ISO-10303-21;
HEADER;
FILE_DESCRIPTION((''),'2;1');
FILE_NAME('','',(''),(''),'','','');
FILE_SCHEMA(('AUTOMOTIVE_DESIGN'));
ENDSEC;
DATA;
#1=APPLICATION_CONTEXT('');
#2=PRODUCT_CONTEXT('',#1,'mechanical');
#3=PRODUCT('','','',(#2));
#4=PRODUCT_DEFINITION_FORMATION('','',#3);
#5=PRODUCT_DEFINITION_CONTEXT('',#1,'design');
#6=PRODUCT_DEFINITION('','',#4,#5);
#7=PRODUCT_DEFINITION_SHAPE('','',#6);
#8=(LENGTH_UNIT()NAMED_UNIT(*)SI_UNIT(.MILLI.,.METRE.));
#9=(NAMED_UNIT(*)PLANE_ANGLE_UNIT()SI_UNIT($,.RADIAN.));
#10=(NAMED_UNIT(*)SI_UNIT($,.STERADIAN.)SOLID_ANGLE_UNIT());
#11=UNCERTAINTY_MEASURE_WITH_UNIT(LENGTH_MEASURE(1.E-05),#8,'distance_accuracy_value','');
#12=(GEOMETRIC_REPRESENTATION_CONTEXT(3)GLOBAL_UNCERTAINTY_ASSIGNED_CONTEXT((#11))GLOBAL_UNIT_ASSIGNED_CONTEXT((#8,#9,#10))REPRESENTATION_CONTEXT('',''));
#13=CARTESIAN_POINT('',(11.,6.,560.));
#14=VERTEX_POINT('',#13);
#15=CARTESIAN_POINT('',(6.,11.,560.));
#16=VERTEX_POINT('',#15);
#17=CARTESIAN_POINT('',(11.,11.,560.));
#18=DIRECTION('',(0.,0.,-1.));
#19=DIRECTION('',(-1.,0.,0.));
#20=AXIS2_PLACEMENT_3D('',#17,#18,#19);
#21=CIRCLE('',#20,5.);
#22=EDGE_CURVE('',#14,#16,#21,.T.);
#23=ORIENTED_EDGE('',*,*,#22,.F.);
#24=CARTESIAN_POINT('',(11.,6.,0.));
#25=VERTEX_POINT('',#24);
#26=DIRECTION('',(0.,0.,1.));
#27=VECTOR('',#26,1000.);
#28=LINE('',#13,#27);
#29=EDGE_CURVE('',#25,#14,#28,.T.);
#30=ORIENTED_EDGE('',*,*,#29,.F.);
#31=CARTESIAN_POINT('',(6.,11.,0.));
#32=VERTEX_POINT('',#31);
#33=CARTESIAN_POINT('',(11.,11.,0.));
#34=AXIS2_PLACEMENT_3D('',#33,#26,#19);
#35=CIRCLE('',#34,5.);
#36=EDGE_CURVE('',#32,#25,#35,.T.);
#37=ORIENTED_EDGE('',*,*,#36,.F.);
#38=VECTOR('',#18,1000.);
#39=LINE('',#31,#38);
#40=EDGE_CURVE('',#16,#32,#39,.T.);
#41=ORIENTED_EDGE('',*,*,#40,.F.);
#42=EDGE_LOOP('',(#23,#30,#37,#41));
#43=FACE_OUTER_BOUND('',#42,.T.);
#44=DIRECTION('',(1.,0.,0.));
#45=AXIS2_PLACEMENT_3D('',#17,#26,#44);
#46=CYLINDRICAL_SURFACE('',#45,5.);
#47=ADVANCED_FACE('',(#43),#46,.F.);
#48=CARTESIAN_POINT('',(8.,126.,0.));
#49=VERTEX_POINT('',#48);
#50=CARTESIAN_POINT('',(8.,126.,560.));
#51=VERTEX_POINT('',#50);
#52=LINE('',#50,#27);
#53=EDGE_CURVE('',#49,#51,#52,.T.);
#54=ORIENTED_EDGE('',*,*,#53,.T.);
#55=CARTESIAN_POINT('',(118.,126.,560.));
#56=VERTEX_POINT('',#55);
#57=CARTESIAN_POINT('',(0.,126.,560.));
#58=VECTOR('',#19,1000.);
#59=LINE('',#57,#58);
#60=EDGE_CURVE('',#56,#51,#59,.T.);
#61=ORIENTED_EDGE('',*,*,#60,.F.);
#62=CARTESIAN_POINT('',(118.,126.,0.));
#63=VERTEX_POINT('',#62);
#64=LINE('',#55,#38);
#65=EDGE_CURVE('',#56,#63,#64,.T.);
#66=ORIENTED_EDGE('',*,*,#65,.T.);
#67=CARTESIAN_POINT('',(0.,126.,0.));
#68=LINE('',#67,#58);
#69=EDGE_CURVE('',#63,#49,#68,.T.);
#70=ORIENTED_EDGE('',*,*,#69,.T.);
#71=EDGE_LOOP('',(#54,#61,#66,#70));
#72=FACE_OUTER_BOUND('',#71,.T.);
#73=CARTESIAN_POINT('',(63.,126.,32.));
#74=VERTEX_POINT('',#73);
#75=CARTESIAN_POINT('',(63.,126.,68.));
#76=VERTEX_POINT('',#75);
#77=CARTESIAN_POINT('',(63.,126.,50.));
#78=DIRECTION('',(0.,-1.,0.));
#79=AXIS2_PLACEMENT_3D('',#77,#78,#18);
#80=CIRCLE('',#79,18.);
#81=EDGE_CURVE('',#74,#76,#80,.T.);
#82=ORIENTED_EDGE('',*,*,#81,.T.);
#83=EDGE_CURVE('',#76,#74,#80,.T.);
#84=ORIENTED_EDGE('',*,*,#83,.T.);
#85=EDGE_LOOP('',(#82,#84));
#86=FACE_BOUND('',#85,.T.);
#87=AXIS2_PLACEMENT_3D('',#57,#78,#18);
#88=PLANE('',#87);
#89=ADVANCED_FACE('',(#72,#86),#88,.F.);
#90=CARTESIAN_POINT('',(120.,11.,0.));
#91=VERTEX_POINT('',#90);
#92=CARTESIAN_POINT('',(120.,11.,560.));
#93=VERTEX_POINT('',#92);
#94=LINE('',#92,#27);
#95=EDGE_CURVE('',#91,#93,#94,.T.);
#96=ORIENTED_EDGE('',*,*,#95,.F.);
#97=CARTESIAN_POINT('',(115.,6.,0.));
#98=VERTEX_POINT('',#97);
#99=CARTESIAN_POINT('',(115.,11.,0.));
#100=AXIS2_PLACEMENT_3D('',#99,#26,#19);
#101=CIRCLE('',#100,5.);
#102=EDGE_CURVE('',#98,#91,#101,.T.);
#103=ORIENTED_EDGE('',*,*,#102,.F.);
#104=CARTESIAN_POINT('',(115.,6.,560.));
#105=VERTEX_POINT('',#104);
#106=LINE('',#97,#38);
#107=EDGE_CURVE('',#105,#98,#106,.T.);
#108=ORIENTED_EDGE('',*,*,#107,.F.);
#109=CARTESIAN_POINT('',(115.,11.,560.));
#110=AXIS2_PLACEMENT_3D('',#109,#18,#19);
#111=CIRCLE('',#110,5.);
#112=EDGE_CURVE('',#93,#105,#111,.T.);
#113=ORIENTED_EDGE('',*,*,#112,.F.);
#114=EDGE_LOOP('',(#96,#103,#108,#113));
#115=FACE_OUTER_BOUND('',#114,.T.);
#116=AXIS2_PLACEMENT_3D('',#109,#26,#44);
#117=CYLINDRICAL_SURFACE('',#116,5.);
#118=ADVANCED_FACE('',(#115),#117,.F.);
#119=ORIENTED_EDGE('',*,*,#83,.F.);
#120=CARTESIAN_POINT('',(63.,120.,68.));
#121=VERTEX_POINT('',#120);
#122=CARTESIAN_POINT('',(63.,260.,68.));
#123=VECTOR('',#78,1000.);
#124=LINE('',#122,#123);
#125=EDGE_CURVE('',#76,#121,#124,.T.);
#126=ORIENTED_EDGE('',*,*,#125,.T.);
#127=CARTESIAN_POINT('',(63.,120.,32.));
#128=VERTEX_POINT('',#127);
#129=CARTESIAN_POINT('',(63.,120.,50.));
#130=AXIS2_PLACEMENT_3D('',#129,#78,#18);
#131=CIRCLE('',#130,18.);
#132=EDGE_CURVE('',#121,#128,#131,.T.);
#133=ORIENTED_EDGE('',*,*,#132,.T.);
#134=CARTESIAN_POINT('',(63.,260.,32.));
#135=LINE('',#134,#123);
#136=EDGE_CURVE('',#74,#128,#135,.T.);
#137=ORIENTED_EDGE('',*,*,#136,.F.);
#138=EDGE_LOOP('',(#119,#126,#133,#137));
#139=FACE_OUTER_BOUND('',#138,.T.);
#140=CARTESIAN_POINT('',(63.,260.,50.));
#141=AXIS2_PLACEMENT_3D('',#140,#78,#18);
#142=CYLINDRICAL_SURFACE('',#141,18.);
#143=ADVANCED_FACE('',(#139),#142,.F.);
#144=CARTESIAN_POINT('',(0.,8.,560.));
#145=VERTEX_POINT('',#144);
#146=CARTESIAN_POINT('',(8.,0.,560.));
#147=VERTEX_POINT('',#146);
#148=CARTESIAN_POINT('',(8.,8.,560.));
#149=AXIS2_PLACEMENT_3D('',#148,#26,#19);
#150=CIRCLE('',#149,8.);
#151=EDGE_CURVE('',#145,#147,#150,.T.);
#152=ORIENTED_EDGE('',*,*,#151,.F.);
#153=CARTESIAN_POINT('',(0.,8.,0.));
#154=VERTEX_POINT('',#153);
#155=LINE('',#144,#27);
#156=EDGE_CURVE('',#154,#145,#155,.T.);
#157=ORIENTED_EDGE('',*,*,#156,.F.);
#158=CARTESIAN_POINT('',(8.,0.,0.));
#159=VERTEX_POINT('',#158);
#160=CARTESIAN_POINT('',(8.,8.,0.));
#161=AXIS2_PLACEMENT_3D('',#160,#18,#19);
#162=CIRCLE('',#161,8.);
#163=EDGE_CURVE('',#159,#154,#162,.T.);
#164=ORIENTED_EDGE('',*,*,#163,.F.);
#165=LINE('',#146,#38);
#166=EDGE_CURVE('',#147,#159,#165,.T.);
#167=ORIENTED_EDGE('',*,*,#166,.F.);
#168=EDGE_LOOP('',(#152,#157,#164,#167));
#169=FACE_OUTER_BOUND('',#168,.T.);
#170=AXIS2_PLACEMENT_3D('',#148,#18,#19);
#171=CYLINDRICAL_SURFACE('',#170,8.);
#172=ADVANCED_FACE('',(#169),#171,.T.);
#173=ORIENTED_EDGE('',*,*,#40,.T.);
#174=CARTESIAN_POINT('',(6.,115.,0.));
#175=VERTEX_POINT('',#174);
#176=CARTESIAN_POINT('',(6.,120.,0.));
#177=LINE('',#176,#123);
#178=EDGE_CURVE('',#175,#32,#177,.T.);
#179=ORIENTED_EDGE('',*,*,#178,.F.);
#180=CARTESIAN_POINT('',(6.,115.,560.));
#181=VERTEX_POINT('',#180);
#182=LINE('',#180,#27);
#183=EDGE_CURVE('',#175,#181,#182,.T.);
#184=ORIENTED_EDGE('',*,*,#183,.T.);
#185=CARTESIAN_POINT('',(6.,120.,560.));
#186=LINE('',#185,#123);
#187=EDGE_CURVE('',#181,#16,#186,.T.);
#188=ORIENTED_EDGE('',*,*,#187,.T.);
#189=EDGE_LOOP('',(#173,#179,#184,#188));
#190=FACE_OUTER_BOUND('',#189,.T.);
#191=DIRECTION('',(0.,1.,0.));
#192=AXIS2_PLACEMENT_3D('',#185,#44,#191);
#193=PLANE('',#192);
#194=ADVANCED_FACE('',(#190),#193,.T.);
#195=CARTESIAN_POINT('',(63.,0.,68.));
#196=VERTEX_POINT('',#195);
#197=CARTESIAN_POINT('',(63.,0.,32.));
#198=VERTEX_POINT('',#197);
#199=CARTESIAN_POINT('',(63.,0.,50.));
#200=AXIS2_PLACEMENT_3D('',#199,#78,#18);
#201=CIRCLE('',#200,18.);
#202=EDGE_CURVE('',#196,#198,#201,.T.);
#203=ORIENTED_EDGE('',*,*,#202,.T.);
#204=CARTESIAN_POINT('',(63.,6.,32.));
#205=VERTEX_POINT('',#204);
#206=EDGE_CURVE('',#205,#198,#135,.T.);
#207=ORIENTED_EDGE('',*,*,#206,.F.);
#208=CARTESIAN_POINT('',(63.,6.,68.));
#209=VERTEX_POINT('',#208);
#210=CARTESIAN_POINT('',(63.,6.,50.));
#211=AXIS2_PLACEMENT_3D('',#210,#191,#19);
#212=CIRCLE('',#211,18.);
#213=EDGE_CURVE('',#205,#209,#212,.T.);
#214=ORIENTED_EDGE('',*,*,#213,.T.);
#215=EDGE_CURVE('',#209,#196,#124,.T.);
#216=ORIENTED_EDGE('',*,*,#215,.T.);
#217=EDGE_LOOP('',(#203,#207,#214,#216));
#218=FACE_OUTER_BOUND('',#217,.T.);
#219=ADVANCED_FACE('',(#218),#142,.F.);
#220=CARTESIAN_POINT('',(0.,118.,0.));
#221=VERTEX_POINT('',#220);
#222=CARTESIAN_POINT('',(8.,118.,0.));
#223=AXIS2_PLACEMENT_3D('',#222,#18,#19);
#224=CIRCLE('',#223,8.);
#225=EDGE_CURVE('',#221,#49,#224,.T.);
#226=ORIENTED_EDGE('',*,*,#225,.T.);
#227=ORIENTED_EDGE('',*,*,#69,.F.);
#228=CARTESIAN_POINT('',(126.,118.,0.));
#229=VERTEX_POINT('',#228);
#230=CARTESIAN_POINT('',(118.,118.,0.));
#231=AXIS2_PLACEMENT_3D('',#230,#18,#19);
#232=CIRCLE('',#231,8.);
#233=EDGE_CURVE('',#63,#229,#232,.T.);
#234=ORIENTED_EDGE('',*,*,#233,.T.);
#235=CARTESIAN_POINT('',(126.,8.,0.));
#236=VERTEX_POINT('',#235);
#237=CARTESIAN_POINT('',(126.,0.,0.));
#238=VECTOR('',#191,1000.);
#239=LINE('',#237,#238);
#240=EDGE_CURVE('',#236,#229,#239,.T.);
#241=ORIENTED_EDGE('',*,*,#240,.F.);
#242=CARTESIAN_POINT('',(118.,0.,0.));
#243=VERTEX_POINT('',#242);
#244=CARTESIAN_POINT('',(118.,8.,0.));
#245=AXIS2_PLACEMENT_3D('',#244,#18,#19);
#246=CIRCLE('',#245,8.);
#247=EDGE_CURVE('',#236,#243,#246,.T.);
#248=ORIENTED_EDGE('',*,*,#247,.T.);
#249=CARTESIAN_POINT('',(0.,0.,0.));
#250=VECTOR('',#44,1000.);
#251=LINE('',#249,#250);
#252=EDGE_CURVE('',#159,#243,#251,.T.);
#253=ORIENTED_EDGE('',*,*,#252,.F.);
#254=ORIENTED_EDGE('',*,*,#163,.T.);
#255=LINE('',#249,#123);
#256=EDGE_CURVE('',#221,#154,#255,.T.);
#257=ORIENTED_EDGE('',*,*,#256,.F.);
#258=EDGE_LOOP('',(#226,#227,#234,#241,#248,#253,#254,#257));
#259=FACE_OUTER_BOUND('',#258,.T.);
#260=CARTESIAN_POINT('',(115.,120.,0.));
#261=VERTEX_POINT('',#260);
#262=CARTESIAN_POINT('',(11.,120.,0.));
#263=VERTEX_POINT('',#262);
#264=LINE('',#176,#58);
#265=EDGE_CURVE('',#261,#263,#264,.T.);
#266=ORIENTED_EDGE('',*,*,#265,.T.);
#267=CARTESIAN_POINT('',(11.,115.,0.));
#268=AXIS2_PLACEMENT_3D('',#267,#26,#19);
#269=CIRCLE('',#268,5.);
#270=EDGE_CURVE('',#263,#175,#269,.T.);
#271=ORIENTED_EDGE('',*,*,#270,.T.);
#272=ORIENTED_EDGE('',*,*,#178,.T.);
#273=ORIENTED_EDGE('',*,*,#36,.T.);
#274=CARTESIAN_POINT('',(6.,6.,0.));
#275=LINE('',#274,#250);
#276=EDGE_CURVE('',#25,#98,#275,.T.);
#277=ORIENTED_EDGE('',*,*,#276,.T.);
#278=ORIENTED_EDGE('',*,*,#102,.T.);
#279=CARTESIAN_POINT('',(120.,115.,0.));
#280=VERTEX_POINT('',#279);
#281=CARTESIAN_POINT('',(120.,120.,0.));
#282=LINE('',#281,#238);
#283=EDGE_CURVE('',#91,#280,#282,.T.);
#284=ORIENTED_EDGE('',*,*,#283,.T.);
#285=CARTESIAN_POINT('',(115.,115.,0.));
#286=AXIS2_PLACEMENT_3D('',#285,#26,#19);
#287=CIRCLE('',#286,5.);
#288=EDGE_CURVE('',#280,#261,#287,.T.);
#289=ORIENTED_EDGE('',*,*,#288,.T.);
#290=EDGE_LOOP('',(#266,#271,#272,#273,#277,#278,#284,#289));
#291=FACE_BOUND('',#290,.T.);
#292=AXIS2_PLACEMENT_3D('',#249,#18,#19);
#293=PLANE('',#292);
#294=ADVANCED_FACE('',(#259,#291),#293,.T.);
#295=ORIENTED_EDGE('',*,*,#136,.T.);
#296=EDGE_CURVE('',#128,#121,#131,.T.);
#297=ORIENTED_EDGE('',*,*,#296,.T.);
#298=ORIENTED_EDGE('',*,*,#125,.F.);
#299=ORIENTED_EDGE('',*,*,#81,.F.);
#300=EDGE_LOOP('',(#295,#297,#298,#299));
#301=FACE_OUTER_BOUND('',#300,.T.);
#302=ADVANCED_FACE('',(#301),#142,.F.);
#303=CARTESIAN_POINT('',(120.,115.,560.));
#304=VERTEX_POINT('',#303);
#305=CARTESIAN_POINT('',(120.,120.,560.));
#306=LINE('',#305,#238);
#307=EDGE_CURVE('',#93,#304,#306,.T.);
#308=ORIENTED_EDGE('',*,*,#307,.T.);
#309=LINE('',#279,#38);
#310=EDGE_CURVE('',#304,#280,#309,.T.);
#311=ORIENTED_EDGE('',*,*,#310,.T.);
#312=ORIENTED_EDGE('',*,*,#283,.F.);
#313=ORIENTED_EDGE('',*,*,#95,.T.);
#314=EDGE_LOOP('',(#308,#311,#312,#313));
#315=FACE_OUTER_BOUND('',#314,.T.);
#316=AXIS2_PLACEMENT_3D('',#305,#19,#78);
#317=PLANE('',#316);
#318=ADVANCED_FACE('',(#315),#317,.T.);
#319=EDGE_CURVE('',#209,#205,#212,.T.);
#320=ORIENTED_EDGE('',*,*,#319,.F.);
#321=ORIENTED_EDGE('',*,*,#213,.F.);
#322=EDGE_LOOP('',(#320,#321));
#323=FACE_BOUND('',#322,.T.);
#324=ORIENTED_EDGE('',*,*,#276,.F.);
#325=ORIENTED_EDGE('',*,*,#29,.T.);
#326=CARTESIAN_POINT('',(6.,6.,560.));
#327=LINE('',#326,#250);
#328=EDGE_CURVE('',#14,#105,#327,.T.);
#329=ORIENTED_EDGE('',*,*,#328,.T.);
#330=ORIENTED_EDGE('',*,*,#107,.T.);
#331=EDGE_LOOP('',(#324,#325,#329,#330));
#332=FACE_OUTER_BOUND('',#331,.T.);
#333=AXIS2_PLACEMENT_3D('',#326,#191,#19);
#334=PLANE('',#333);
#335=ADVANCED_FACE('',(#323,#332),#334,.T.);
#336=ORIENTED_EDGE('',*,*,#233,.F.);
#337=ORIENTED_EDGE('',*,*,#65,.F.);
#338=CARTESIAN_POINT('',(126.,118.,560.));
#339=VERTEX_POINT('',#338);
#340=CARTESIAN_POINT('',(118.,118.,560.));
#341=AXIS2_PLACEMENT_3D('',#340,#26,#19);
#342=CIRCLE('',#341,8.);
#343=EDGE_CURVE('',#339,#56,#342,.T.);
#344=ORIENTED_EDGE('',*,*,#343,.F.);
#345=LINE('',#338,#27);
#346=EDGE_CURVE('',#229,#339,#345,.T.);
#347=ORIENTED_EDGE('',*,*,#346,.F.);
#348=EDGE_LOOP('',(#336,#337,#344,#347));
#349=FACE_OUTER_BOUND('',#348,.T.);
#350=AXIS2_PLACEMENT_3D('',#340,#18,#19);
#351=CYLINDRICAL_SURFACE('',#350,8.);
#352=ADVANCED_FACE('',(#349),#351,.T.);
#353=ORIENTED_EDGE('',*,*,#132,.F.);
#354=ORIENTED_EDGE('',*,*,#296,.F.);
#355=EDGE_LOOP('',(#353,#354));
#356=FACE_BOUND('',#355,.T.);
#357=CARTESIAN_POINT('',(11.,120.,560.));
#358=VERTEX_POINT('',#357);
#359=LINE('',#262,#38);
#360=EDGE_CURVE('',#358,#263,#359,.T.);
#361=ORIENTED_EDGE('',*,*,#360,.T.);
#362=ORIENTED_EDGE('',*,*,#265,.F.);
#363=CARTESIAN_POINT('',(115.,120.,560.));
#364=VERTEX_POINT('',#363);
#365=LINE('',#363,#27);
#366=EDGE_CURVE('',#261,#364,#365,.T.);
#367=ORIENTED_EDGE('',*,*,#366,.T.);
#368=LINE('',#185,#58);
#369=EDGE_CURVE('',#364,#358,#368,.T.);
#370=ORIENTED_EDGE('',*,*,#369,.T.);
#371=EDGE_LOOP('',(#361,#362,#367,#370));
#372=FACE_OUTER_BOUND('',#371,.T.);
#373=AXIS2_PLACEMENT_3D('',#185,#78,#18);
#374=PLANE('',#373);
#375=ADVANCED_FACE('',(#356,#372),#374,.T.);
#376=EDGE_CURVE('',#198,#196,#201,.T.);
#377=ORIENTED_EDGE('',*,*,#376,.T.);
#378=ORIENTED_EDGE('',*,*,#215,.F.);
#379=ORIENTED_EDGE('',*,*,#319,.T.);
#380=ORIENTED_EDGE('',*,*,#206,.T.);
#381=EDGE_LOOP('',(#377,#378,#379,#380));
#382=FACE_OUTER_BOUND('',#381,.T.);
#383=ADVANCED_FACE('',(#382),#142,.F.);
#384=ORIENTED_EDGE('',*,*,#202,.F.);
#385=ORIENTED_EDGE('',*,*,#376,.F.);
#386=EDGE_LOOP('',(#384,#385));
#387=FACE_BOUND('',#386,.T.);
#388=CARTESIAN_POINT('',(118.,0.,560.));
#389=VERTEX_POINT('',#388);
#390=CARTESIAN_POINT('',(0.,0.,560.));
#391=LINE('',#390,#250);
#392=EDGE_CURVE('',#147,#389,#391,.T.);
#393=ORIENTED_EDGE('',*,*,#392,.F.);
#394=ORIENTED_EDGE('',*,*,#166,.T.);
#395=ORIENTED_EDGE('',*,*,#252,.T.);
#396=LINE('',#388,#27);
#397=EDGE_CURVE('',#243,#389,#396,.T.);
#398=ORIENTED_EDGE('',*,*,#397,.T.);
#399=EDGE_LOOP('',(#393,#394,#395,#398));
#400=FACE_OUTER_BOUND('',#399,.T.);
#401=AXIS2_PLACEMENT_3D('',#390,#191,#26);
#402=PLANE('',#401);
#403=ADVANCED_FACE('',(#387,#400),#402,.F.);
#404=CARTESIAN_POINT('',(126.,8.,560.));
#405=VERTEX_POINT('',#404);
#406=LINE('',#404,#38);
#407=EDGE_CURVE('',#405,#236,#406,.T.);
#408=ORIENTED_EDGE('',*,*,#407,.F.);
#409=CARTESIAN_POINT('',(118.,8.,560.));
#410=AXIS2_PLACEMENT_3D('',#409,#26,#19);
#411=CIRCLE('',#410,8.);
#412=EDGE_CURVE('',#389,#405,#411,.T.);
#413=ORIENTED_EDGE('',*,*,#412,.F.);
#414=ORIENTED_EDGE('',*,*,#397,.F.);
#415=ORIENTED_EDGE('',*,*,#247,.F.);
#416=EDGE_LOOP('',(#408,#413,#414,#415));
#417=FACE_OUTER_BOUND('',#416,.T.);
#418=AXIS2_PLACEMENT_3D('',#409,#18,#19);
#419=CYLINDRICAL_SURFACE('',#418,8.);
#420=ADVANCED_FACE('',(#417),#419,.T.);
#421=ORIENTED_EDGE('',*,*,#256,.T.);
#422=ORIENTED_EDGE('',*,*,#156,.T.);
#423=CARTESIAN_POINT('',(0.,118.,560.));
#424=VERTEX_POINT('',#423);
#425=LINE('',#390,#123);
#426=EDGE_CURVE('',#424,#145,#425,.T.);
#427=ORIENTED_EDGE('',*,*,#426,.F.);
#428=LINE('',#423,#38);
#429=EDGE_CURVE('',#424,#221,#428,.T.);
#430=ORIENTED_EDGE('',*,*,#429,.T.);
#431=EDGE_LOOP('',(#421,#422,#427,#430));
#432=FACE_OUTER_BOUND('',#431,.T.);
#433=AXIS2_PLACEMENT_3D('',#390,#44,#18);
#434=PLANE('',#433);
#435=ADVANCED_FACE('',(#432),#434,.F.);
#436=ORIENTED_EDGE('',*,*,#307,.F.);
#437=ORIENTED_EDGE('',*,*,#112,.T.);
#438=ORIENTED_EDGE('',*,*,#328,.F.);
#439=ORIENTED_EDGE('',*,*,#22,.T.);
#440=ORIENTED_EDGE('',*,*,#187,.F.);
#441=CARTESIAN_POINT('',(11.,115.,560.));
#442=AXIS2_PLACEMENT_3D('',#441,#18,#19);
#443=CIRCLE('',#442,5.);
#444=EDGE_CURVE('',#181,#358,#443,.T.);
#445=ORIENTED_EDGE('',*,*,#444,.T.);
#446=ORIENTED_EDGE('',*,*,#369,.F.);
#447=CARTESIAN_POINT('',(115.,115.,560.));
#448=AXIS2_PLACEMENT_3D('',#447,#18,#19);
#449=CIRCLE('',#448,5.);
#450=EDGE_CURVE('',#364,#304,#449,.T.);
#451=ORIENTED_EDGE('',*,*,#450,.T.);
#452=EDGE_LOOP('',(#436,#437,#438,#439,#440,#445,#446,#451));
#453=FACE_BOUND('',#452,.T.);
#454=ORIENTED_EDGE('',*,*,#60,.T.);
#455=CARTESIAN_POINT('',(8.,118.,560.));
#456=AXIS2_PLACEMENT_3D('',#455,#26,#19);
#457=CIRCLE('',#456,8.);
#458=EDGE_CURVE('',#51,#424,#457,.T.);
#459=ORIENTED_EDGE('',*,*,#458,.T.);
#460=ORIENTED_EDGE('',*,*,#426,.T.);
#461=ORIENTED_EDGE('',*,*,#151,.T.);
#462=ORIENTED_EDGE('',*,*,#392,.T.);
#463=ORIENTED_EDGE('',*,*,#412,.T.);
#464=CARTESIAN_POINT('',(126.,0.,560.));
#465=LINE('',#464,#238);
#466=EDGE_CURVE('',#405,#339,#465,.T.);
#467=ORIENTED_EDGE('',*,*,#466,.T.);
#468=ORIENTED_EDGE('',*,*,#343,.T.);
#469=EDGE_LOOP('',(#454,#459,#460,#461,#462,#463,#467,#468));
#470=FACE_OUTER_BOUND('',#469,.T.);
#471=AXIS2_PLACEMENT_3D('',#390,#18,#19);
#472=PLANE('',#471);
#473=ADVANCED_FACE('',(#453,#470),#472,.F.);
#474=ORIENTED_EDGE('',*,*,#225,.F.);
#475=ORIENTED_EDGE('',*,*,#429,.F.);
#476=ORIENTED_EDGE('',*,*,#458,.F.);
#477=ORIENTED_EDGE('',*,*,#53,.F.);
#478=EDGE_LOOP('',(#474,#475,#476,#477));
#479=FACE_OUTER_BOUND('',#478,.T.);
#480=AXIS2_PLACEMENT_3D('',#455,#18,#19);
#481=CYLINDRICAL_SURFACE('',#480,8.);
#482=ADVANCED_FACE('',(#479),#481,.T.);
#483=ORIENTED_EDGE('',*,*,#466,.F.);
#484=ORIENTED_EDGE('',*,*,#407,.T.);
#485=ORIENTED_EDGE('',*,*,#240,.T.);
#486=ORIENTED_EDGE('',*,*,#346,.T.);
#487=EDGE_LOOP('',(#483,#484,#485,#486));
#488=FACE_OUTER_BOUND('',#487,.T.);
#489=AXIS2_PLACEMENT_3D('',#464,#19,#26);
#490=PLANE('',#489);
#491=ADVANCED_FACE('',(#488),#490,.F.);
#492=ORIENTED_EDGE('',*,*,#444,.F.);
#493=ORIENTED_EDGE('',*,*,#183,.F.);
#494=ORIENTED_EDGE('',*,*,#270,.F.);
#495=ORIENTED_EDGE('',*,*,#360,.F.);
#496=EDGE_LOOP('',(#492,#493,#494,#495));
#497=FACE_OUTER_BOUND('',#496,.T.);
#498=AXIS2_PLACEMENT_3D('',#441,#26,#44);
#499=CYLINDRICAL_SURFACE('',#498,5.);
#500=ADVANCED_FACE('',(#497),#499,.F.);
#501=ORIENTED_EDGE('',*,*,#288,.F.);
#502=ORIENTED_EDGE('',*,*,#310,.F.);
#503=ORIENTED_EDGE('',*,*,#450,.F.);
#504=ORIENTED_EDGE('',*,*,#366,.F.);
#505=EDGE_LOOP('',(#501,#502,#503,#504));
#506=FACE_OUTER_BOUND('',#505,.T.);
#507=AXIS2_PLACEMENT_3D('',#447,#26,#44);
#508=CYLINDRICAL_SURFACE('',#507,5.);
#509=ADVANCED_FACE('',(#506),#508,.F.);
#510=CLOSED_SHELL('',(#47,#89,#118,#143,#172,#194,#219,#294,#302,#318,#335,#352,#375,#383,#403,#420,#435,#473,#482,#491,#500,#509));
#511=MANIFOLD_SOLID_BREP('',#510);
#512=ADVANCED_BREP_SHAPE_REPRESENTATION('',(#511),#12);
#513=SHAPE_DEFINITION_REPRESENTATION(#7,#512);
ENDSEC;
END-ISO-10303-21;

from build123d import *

# Parameters (mm, degrees)
SKETCH1_W           = 126
SKETCH1_H           = 126
SKETCH1_W_2         = 114
SKETCH1_H_2         = 114
BOSS_EXTRUDE1_DEPTH = 560
FILLET1_R           = 8
FILLET2_R           = 5
SKETCH3_R           = 18
CUT_EXTRUDE1_DEPTH  = 260


with BuildPart() as part:
    # Sketch1 → Boss-Extrude1 (new body)
    with BuildSketch(Plane.XY):
        with Locations((63, 63)):
            Rectangle(SKETCH1_W, SKETCH1_H)
        with Locations((63, 63)):
            Rectangle(SKETCH1_W_2, SKETCH1_H_2, mode=Mode.SUBTRACT)
    extrude(amount=BOSS_EXTRUDE1_DEPTH)

    # Fillet1
    fillet1_edges = [part.edges().sort_by_distance(p)[0] for p in [
        (0, 126, 280),
        (126, 126, 280),
        (126, 0, 280),
        (0, 0, 280),
    ]]
    fillet(fillet1_edges, radius=FILLET1_R)

    # Fillet2
    fillet2_edges = [part.edges().sort_by_distance(p)[0] for p in [
        (6, 120, 280),
        (6, 6, 280),
        (120, 6, 280),
        (120, 120, 280),
    ]]
    fillet(fillet2_edges, radius=FILLET2_R)

    # Sketch3 → Cut-Extrude1 (cut)
    with BuildSketch(Plane.XZ):
        with Locations(Location((63, 50, 0), (0, 0, 270))):
            Circle(SKETCH3_R)
    extrude(amount=-CUT_EXTRUDE1_DEPTH, mode=Mode.SUBTRACT)


solid = part.part
